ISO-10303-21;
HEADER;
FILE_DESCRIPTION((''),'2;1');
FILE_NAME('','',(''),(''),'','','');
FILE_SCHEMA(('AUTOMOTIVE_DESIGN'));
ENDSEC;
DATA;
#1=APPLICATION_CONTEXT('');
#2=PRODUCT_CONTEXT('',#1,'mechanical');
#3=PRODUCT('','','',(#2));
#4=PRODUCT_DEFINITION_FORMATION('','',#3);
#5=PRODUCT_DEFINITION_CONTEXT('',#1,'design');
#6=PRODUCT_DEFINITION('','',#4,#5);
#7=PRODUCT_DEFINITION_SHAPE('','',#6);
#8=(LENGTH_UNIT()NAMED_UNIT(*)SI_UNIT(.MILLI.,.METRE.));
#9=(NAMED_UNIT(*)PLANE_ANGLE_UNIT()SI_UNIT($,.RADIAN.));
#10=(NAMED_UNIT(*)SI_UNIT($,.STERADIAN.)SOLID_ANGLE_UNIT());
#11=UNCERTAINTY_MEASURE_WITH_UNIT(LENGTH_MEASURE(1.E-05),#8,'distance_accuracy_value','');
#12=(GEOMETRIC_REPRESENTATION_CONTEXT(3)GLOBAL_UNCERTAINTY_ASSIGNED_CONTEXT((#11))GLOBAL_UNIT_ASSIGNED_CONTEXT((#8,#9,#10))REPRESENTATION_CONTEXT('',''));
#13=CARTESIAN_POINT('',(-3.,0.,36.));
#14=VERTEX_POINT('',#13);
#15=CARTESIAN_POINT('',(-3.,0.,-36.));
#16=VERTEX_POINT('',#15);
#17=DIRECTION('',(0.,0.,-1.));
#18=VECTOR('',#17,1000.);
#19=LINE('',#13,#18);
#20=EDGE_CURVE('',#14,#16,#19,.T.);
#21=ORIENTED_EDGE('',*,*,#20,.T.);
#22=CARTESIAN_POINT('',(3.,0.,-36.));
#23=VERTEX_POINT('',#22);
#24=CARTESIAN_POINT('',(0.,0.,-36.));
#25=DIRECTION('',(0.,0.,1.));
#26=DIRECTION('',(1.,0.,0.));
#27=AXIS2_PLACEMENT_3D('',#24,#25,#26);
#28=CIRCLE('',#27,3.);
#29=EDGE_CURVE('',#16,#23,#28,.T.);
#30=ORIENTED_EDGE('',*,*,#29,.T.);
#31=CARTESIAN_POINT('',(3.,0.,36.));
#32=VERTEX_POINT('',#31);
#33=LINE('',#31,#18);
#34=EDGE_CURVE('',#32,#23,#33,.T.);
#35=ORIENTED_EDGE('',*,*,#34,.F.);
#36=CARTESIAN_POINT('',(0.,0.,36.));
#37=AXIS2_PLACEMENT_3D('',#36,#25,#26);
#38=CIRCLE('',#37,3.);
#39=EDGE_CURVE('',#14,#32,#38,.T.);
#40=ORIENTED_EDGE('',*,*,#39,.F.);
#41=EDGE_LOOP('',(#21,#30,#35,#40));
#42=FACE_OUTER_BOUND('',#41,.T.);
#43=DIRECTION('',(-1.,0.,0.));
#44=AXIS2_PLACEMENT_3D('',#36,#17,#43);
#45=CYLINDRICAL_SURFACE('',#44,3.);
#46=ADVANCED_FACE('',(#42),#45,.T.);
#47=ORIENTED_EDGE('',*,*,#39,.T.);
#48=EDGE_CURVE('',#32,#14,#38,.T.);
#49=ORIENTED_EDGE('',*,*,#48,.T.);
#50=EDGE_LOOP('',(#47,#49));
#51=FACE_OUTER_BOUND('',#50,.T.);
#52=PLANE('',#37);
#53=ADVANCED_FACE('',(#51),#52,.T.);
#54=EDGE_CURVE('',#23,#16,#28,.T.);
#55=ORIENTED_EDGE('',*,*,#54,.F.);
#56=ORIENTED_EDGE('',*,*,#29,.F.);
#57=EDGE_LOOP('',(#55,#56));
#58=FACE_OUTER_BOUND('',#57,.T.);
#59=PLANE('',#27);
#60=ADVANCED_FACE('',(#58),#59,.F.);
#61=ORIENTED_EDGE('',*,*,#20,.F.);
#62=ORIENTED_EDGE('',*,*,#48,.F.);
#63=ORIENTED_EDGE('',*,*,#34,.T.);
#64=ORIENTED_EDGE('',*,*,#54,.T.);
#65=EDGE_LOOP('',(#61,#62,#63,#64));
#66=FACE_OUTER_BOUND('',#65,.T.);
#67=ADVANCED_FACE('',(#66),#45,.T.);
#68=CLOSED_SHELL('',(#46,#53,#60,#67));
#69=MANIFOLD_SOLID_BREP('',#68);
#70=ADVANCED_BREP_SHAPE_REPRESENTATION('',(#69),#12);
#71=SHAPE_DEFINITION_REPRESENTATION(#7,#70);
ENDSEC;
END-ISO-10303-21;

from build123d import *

# Parameters (mm, degrees)
PIN_PROFILE_6_R     = 3
PIN_BODY_6X72_DEPTH = 36


with BuildPart() as part:
    # Pin Profile Ø6 → Pin Body Ø6x72 (new, symmetric)
    with BuildSketch(Plane.XY):
        Circle(PIN_PROFILE_6_R)
    extrude(amount=PIN_BODY_6X72_DEPTH, both=True)


solid = part.part
